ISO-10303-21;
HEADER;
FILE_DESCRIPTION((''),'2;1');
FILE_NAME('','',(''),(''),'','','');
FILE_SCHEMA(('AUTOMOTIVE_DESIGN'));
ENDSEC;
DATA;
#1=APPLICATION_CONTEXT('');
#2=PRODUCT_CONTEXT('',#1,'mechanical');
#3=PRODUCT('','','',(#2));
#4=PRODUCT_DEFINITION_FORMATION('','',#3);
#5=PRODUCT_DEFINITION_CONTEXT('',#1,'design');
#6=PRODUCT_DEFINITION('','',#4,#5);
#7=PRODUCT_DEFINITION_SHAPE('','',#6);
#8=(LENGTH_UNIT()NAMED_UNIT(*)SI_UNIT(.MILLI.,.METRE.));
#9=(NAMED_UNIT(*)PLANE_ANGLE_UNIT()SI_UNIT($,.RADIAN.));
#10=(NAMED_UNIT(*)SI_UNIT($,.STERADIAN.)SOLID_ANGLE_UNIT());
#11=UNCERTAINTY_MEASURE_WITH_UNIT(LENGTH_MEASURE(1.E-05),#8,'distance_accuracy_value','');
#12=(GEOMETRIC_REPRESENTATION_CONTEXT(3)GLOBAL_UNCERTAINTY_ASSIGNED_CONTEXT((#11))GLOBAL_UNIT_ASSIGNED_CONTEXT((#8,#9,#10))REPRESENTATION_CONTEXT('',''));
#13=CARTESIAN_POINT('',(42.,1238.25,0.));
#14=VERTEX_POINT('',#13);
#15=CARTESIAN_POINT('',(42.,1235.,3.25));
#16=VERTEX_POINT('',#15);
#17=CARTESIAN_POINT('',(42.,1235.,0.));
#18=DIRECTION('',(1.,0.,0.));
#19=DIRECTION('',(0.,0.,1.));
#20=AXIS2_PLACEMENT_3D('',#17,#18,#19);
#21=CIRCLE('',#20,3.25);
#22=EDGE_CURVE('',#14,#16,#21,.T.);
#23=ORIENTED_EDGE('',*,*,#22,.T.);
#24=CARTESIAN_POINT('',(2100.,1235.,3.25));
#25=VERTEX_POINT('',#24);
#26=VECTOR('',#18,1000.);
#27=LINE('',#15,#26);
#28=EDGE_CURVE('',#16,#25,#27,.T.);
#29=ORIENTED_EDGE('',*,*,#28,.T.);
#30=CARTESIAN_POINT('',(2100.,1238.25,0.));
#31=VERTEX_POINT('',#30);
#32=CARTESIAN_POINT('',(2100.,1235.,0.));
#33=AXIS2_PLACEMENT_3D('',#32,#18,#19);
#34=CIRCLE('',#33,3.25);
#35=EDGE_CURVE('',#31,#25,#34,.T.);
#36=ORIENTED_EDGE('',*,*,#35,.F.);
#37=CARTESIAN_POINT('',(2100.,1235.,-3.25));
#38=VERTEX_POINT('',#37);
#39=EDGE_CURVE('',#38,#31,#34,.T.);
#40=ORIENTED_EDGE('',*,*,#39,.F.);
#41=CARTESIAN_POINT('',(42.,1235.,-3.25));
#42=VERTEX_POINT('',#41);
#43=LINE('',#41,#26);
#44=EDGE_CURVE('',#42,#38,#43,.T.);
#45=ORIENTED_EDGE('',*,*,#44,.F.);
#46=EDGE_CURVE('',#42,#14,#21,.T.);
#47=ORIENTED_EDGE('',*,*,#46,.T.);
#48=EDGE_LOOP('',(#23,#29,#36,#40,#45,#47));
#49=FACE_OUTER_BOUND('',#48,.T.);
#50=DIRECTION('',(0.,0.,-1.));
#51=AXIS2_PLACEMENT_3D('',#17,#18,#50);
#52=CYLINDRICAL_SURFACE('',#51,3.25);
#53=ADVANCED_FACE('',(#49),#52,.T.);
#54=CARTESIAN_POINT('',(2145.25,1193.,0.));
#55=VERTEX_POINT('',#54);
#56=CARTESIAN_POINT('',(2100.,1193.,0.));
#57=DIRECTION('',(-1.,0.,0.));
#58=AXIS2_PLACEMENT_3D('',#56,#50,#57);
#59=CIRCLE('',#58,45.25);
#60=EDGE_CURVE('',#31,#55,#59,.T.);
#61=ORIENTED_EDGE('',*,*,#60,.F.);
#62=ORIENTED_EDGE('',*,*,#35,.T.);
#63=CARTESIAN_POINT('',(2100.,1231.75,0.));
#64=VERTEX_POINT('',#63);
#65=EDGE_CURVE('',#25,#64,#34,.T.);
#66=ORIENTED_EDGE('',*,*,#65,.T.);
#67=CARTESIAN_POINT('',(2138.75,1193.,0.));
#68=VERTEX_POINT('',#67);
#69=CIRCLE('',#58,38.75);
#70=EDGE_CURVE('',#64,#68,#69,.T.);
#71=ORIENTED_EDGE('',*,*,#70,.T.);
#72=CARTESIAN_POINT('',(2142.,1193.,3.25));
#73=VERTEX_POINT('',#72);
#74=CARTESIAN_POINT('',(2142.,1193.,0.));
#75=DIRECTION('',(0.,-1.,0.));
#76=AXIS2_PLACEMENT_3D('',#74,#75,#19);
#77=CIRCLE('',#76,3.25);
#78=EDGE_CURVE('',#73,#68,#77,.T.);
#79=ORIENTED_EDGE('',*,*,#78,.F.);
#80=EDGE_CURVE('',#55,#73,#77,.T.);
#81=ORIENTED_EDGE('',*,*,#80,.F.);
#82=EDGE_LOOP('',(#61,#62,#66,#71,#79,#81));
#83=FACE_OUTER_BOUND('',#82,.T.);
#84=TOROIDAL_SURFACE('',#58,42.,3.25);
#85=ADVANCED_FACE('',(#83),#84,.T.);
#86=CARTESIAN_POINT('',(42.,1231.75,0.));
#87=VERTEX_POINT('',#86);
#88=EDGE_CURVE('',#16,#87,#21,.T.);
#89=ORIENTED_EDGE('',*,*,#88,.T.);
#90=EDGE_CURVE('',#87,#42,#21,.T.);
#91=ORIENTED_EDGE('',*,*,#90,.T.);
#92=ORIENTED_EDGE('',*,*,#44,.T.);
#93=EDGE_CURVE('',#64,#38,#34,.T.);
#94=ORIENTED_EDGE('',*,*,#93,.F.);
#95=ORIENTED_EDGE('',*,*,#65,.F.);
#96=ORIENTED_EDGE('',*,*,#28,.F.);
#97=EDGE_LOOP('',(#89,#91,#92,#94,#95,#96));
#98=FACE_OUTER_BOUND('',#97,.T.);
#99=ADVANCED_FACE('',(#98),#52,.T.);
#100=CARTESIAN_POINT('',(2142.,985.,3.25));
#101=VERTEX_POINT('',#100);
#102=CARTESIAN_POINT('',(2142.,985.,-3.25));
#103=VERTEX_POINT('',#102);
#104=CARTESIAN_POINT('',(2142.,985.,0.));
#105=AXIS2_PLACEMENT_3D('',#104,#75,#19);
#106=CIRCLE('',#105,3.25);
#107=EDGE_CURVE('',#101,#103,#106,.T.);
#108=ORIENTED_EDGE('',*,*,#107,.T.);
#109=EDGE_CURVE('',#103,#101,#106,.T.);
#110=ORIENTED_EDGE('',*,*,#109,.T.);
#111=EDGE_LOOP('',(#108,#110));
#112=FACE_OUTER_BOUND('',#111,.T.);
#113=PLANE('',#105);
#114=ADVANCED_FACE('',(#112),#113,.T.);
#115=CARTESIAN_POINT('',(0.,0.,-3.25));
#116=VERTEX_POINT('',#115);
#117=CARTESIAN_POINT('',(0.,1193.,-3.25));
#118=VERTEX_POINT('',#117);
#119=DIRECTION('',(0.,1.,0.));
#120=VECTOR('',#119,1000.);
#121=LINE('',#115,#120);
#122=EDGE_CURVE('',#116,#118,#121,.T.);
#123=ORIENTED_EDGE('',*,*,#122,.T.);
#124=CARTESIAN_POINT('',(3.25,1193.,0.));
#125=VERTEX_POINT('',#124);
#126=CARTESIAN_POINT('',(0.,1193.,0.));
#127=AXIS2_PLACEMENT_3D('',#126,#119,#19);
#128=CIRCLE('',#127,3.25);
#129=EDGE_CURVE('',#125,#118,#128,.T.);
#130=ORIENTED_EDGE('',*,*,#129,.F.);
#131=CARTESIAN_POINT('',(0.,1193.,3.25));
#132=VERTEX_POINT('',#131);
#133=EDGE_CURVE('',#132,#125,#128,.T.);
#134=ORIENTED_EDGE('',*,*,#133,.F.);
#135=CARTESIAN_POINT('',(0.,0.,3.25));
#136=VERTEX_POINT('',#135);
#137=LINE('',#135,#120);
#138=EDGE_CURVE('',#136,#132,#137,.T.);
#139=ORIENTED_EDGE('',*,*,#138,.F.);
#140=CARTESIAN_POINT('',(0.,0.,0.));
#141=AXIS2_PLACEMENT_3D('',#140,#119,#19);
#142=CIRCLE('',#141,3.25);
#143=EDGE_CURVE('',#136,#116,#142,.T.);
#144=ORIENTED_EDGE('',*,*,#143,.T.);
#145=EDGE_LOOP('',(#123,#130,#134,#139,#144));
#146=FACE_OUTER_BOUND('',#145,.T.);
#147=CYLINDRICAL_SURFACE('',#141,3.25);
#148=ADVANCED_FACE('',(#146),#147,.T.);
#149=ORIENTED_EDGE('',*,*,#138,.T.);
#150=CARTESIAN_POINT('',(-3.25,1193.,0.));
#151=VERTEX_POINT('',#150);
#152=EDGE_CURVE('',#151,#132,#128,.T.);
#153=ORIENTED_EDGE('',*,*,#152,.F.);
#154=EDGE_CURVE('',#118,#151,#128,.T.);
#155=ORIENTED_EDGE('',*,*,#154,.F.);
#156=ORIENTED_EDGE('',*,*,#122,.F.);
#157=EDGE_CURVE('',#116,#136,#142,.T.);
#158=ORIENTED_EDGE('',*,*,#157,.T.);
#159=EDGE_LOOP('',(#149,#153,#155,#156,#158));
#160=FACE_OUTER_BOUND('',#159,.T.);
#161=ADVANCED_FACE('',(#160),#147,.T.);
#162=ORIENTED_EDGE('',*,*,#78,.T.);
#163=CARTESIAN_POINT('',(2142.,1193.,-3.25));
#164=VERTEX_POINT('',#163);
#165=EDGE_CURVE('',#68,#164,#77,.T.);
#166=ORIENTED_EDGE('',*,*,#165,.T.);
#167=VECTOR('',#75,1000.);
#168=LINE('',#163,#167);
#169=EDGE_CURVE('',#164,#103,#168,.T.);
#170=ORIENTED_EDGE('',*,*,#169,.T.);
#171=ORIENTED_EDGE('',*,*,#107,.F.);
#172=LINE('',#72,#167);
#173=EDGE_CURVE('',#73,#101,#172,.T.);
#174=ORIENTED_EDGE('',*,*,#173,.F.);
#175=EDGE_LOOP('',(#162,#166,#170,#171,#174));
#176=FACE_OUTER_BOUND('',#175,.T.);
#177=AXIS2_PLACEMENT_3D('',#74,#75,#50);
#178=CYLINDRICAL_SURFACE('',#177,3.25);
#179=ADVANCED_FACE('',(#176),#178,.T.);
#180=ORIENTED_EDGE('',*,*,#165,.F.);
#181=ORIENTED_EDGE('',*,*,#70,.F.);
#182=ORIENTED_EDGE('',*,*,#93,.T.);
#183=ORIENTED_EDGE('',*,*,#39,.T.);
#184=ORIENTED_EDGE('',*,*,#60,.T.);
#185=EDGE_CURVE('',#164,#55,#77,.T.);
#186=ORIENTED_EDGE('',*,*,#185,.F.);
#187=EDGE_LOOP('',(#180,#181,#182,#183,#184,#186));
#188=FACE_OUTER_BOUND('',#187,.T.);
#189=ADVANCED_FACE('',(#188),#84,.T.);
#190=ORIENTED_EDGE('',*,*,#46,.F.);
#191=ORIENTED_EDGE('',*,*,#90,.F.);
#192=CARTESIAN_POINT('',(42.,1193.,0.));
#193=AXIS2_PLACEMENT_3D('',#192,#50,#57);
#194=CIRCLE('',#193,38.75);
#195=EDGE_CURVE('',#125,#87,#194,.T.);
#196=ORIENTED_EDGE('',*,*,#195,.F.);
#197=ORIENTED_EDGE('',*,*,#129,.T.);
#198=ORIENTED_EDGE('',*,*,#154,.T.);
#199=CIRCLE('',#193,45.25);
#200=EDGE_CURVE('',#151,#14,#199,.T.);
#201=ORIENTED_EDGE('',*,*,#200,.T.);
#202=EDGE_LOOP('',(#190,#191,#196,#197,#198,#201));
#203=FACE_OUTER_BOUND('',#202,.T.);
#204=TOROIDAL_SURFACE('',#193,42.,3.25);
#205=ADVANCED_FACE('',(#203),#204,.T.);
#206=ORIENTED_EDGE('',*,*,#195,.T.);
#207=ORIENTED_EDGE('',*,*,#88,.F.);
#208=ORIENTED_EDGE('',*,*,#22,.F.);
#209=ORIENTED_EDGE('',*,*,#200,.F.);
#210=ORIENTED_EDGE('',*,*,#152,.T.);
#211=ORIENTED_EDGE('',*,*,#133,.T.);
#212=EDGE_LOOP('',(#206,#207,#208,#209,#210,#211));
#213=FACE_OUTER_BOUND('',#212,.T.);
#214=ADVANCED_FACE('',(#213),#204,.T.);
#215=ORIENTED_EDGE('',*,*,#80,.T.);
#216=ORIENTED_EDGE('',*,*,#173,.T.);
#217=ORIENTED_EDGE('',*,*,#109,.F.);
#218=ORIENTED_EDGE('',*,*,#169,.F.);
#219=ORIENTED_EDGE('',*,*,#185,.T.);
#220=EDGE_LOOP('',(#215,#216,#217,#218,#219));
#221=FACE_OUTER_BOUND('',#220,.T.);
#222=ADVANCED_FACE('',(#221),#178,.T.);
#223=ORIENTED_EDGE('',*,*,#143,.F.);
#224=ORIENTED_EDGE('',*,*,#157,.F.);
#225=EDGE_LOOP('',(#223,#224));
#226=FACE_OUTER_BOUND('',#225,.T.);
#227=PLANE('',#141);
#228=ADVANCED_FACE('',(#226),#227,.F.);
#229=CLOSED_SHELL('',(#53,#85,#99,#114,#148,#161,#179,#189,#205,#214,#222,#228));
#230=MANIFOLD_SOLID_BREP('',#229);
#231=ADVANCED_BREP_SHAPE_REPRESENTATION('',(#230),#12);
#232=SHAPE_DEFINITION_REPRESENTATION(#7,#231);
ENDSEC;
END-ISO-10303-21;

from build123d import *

# Parameters (mm, degrees)
SKETCH2_R = 3.25


with BuildPart() as part:
    # Sweep1: sweep along a path in Sketch1
    with BuildLine(Plane.XY) as sweep1_path:
        Line((0, 0), (0, 1193))
        ThreePointArc((0, 1193), (12.30151519, 1222.69848481), (42, 1235))
        Line((42, 1235), (2100, 1235))
        ThreePointArc((2100, 1235), (2129.69848481, 1222.69848481), (2142, 1193))
        Line((2142, 1193), (2142, 985))
    # Sketch2 → Sweep1 (sweep)
    with BuildSketch(Plane(origin=(0, 0, 0), x_dir=(1, 0, 0), z_dir=(0, 1, 0))):
        Circle(SKETCH2_R)
    sweep(path=sweep1_path.line)


solid = part.part
